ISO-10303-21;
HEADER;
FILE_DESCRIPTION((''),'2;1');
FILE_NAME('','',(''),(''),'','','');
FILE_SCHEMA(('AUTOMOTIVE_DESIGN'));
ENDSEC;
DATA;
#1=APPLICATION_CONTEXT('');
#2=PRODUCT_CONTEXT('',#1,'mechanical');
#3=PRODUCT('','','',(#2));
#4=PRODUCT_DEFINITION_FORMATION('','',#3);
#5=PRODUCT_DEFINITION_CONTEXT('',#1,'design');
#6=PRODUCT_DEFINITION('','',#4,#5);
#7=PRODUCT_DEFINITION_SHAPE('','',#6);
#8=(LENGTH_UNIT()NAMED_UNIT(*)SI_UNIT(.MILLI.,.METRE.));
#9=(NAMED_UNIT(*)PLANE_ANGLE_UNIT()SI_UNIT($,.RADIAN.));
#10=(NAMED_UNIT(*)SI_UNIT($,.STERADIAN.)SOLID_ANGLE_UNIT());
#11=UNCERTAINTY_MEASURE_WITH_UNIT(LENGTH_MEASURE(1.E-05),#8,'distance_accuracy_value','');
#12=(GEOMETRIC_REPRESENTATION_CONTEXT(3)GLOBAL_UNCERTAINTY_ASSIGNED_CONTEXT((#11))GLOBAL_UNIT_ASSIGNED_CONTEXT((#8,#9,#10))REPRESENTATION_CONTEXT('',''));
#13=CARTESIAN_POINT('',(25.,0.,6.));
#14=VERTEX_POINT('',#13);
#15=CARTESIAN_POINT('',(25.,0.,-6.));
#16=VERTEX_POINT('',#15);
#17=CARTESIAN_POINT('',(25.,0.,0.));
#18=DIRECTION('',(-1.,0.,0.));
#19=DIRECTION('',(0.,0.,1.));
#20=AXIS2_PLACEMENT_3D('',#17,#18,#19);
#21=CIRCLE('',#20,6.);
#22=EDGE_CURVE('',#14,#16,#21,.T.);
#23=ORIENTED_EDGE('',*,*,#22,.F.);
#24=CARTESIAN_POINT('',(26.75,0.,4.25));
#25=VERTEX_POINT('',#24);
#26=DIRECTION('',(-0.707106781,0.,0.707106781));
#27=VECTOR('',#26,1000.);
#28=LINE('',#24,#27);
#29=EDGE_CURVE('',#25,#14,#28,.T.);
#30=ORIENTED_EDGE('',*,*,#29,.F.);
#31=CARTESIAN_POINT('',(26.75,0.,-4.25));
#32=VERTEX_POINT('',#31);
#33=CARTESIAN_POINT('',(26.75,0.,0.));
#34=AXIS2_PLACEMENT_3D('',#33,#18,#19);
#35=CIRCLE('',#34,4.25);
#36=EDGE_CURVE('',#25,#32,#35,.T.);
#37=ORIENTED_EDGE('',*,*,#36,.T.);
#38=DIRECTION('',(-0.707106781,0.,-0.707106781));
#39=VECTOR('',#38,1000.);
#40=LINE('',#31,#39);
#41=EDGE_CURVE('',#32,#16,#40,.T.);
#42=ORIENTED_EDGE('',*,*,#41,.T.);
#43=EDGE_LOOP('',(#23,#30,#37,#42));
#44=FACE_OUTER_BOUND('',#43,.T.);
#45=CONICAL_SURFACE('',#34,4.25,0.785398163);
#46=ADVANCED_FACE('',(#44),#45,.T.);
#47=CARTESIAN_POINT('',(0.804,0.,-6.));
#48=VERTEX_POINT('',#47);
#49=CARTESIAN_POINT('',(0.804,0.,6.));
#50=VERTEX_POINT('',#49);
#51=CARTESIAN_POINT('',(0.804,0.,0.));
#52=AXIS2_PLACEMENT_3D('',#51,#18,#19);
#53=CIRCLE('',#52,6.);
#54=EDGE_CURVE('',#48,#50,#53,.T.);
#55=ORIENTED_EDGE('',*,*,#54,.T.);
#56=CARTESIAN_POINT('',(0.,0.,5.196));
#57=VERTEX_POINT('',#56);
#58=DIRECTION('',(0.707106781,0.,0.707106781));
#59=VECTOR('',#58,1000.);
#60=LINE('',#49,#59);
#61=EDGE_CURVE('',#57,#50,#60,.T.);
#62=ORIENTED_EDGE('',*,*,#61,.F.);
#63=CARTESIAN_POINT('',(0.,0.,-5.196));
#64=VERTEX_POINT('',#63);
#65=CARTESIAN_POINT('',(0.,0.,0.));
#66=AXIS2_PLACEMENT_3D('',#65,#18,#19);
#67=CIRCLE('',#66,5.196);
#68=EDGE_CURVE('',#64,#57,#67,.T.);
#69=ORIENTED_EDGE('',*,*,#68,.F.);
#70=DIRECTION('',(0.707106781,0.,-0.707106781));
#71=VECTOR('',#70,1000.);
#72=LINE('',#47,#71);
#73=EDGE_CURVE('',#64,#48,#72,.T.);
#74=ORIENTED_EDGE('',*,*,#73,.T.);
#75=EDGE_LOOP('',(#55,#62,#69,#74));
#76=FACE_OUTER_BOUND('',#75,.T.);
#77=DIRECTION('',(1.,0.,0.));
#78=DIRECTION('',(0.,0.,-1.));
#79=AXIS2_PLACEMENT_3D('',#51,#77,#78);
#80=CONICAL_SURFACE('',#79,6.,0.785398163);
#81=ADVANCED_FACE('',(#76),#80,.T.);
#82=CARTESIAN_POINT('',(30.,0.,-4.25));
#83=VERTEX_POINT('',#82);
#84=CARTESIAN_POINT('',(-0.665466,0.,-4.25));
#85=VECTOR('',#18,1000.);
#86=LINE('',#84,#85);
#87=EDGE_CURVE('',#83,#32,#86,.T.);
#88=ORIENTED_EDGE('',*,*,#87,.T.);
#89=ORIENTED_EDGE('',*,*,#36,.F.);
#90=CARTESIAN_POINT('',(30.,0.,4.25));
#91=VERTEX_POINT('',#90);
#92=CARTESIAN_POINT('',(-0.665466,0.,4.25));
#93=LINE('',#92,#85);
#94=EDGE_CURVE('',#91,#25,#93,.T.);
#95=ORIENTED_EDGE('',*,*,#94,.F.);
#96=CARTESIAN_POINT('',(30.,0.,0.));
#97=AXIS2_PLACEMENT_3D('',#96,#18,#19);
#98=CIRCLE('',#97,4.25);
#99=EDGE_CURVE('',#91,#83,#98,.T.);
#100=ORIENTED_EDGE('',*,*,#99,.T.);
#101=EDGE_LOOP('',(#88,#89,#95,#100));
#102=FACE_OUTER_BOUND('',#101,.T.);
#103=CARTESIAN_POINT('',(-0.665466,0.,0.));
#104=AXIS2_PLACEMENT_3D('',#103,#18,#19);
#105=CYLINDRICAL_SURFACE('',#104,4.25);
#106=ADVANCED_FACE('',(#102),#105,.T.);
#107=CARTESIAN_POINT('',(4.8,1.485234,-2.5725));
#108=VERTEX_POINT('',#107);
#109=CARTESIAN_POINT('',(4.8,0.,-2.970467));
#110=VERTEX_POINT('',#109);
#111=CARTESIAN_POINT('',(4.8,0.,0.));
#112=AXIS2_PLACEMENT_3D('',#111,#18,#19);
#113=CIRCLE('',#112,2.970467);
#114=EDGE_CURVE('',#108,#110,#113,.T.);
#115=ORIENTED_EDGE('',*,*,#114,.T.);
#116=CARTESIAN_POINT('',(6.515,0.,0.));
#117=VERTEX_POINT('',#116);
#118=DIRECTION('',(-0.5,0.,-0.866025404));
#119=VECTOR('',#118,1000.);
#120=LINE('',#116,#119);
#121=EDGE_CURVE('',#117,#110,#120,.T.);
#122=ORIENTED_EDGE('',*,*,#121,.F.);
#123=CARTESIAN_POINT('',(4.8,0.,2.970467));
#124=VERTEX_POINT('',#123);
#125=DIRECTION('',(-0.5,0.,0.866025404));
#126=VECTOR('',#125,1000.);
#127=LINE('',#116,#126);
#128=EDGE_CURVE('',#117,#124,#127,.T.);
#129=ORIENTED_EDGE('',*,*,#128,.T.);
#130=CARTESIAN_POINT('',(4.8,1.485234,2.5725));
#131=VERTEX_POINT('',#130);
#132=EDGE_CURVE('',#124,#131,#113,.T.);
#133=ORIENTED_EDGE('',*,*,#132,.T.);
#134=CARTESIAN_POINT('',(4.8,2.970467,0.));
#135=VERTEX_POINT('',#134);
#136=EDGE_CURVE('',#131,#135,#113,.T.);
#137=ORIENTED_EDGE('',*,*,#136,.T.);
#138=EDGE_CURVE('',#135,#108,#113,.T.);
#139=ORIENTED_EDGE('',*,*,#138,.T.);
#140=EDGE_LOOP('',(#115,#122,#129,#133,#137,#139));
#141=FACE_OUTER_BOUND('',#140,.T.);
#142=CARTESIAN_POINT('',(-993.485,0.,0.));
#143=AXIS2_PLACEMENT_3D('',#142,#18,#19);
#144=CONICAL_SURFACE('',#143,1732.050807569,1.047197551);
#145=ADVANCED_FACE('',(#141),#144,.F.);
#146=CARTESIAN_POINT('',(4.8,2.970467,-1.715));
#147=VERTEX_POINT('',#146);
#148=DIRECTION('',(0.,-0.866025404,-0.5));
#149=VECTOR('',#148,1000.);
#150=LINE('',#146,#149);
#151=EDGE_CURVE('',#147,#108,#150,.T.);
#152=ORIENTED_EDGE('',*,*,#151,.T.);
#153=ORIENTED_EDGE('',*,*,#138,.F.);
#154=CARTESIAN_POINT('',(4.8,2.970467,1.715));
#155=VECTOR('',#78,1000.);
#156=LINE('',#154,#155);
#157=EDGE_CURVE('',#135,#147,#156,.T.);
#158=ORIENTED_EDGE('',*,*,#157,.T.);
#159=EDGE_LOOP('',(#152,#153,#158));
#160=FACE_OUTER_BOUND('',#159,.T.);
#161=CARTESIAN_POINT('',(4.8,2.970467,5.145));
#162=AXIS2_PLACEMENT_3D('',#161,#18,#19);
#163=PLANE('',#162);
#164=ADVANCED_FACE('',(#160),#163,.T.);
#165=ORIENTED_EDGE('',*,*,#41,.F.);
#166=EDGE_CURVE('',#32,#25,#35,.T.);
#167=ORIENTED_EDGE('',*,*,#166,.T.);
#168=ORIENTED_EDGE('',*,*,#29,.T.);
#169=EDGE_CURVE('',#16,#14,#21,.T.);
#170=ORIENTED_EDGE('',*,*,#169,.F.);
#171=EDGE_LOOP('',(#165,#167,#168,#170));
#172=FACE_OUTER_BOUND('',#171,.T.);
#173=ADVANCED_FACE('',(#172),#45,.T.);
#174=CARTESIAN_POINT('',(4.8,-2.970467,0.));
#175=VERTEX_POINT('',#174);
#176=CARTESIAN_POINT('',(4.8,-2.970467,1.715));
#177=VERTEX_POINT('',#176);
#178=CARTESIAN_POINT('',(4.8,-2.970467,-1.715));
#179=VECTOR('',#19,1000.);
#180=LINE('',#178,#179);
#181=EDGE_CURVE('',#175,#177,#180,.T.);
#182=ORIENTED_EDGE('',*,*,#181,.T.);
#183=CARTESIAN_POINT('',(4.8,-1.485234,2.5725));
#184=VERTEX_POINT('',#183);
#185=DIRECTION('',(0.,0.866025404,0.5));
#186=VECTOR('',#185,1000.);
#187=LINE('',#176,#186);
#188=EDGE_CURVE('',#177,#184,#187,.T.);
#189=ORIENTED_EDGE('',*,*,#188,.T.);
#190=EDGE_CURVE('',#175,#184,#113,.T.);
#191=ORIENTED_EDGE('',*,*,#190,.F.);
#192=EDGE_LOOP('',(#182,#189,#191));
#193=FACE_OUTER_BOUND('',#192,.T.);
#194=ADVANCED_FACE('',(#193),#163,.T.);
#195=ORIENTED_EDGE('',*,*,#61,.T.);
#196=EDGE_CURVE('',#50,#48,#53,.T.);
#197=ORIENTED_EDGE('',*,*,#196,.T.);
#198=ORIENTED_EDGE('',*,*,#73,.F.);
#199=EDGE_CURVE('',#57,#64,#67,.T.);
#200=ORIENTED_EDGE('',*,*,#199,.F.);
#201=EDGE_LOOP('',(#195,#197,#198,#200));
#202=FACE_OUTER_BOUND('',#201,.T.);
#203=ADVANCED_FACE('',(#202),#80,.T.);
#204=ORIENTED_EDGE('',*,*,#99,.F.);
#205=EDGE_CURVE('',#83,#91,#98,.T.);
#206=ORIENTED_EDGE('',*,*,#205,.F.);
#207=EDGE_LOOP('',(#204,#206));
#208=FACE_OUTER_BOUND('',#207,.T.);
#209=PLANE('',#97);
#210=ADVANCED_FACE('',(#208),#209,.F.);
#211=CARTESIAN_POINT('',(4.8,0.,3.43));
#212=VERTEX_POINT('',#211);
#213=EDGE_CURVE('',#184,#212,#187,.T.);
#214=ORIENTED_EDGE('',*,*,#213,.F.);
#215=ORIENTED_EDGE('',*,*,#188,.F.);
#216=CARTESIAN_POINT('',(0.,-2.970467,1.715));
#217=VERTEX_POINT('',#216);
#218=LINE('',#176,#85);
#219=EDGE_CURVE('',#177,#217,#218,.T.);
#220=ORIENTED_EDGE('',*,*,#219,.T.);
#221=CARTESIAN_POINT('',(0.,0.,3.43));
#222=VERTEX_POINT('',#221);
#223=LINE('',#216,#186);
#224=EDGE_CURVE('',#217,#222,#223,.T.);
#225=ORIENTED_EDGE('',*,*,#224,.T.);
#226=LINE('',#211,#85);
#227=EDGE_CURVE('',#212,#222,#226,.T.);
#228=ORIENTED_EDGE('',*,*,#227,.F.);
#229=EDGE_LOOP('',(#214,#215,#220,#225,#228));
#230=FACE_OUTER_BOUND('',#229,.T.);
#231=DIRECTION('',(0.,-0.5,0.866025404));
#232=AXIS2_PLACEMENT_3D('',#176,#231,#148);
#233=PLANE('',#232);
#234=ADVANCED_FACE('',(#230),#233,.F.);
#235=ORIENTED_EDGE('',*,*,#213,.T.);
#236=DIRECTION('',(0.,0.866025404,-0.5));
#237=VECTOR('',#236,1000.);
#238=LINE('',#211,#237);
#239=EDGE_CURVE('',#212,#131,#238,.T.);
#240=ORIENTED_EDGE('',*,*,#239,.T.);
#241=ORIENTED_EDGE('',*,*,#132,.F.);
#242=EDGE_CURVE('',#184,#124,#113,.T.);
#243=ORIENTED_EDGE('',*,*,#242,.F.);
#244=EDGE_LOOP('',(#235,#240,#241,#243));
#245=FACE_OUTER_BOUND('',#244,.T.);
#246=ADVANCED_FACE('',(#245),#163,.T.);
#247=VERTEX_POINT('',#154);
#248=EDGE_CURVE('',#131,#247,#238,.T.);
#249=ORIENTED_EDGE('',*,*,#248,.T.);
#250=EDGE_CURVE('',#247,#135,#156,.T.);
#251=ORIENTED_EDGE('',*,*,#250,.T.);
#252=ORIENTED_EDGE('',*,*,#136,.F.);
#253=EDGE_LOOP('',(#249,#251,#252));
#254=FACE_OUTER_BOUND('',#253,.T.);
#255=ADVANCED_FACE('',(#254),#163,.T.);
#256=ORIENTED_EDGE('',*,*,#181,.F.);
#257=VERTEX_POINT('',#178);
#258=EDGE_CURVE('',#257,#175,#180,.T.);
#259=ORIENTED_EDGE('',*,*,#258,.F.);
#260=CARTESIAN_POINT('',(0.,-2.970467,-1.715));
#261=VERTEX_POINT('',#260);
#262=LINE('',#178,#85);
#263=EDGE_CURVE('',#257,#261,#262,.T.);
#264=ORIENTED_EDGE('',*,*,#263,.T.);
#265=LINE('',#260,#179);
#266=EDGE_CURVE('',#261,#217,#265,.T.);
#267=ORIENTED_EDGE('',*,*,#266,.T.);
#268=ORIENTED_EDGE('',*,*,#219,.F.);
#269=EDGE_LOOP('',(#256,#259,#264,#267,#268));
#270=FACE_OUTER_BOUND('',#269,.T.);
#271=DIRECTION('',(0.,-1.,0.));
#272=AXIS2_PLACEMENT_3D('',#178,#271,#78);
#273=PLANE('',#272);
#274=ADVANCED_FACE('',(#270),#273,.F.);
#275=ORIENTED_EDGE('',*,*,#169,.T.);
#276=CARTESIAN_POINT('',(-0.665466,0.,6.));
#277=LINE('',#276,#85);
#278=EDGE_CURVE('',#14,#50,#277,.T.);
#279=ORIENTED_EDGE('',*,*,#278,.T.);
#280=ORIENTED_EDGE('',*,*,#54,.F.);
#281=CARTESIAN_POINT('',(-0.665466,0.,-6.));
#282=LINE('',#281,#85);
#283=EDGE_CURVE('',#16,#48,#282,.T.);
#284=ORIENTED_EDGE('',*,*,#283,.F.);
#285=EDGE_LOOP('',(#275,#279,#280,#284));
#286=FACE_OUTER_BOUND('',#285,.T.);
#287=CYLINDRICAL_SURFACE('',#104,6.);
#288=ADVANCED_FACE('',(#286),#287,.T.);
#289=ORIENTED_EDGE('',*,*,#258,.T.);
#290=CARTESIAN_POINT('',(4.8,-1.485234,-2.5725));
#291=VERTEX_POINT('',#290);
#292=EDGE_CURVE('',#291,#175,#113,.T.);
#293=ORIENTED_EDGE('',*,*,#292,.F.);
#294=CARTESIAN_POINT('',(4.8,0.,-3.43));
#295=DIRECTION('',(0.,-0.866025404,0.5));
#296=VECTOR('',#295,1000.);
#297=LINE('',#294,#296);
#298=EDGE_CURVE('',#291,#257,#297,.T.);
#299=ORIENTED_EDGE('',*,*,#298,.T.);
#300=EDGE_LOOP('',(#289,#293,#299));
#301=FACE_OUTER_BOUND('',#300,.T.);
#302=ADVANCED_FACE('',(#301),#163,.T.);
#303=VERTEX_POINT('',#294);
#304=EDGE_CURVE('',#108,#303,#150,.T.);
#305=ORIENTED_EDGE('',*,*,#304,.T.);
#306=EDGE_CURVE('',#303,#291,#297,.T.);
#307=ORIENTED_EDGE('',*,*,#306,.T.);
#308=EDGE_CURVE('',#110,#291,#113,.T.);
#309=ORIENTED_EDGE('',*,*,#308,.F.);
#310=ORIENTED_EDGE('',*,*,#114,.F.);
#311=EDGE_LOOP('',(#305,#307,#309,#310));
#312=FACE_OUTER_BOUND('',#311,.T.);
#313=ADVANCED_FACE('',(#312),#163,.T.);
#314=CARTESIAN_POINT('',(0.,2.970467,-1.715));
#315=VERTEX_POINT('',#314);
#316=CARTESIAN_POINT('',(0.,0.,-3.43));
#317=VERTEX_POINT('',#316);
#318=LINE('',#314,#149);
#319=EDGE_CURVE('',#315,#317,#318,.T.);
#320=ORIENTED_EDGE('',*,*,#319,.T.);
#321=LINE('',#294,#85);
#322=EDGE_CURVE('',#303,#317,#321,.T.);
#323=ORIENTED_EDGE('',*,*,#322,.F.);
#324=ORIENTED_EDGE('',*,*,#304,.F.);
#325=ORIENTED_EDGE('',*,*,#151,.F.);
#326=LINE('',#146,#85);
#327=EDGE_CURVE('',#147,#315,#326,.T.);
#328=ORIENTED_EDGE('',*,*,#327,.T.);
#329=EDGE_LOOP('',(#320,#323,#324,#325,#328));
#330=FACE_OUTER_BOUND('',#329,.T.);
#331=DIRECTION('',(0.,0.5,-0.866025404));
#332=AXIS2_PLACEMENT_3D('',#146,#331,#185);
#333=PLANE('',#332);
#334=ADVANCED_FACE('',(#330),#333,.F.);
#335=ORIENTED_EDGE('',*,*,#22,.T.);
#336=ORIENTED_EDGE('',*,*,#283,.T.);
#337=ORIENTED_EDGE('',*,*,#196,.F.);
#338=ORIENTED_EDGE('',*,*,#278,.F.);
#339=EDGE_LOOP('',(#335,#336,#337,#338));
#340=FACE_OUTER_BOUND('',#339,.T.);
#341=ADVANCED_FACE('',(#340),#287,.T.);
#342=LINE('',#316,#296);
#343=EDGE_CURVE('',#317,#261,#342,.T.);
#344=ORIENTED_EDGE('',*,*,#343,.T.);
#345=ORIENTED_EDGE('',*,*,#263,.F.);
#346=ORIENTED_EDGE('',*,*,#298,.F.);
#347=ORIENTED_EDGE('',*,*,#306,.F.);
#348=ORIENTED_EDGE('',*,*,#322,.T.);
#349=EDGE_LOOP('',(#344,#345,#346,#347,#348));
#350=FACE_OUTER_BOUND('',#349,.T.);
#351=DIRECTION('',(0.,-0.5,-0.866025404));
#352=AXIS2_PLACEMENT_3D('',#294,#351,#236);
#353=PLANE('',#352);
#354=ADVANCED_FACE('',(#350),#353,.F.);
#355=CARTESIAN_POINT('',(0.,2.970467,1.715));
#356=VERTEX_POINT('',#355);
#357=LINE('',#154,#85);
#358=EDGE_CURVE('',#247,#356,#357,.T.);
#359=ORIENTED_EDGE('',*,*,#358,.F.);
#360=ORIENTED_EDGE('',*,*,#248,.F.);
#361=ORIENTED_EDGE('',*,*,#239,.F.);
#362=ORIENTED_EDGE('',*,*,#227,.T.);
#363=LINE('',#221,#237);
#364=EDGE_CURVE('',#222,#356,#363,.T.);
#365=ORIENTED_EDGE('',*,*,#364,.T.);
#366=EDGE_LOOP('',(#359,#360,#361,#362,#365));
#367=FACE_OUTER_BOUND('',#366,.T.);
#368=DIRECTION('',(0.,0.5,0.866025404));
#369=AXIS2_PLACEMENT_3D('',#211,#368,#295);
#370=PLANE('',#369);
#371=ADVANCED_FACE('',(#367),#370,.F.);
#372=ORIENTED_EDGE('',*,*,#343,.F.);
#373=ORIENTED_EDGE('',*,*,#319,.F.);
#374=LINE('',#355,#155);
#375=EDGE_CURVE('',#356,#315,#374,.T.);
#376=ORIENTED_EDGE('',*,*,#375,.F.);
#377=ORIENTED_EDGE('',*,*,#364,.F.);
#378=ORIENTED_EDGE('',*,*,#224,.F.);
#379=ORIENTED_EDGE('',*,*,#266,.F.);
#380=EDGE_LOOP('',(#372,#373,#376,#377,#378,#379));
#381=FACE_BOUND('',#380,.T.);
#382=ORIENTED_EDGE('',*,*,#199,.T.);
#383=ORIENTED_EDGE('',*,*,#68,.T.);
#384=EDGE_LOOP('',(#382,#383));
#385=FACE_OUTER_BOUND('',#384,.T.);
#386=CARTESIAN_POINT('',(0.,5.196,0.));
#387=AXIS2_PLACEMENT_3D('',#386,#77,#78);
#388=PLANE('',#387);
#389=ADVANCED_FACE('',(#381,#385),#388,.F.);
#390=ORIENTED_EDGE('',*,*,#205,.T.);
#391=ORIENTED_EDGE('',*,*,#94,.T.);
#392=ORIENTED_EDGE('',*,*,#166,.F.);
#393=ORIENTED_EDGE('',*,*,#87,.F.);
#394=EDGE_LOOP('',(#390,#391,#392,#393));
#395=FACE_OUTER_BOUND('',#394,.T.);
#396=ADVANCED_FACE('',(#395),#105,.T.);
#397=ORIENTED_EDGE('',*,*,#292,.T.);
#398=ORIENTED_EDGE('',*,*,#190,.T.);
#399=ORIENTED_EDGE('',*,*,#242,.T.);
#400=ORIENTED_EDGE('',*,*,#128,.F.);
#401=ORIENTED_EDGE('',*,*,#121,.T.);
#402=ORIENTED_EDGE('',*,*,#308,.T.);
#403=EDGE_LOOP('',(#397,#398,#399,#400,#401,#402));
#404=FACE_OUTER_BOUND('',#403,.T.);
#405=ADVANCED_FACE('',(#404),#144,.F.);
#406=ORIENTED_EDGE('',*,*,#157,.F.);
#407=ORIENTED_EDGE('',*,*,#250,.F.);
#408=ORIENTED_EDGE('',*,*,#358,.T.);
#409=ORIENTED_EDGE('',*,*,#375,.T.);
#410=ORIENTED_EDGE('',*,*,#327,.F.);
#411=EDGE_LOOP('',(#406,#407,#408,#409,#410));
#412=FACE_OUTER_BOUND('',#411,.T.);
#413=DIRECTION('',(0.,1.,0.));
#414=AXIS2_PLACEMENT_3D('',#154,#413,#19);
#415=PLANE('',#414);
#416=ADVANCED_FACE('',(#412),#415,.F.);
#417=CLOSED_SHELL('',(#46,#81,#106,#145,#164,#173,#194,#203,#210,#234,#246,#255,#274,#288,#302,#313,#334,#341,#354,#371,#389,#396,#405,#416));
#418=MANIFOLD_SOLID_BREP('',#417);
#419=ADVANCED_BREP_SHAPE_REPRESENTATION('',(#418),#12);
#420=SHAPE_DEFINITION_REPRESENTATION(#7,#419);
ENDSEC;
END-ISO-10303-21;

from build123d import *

# Parameters (mm, degrees)
CUT_EXTRUDE_1_DEPTH = 4.8


with BuildPart() as part:
    # 草图1 → Revolve 598 (revolve)
    with BuildSketch(Plane.XY, mode=Mode.PRIVATE) as revolve_598_sk:
        Polygon((0, 0), (30, 0), (30, 4.25), (26.75, 4.25), (25, 6), (0.804, 6), (0, 5.196), align=None)
    revolve(revolve_598_sk.sketch.rotate(Axis((-0.665465891, 0, 0), (1, 0, 0)), 90), axis=Axis((-0.665465891, 0, 0), (1, 0, 0)))

    # 草图2 → 切除-拉伸1 (cut)
    with BuildSketch(Plane.ZY):
        Polygon((3.43, 0), (1.715, 2.970467135), (-1.715, 2.970467135), (-3.43, 0), (-1.715, -2.970467135), (1.715, -2.970467135), align=None)
    extrude(amount=-CUT_EXTRUDE_1_DEPTH, mode=Mode.SUBTRACT)

    # 草图3 → 切除-旋转1 (revolve, cut)
    with BuildSketch(Plane.XY, mode=Mode.PRIVATE) as cut_revolve_1_sk:
        Polygon((4.8, 2.970467135), (6.515, 0), (4.8, 0), align=None)
    revolve(cut_revolve_1_sk.sketch.rotate(Axis((-0.262128326, 0, 0), (1, 0, 0)), 90), axis=Axis((-0.262128326, 0, 0), (1, 0, 0)), mode=Mode.SUBTRACT)


solid = part.part
